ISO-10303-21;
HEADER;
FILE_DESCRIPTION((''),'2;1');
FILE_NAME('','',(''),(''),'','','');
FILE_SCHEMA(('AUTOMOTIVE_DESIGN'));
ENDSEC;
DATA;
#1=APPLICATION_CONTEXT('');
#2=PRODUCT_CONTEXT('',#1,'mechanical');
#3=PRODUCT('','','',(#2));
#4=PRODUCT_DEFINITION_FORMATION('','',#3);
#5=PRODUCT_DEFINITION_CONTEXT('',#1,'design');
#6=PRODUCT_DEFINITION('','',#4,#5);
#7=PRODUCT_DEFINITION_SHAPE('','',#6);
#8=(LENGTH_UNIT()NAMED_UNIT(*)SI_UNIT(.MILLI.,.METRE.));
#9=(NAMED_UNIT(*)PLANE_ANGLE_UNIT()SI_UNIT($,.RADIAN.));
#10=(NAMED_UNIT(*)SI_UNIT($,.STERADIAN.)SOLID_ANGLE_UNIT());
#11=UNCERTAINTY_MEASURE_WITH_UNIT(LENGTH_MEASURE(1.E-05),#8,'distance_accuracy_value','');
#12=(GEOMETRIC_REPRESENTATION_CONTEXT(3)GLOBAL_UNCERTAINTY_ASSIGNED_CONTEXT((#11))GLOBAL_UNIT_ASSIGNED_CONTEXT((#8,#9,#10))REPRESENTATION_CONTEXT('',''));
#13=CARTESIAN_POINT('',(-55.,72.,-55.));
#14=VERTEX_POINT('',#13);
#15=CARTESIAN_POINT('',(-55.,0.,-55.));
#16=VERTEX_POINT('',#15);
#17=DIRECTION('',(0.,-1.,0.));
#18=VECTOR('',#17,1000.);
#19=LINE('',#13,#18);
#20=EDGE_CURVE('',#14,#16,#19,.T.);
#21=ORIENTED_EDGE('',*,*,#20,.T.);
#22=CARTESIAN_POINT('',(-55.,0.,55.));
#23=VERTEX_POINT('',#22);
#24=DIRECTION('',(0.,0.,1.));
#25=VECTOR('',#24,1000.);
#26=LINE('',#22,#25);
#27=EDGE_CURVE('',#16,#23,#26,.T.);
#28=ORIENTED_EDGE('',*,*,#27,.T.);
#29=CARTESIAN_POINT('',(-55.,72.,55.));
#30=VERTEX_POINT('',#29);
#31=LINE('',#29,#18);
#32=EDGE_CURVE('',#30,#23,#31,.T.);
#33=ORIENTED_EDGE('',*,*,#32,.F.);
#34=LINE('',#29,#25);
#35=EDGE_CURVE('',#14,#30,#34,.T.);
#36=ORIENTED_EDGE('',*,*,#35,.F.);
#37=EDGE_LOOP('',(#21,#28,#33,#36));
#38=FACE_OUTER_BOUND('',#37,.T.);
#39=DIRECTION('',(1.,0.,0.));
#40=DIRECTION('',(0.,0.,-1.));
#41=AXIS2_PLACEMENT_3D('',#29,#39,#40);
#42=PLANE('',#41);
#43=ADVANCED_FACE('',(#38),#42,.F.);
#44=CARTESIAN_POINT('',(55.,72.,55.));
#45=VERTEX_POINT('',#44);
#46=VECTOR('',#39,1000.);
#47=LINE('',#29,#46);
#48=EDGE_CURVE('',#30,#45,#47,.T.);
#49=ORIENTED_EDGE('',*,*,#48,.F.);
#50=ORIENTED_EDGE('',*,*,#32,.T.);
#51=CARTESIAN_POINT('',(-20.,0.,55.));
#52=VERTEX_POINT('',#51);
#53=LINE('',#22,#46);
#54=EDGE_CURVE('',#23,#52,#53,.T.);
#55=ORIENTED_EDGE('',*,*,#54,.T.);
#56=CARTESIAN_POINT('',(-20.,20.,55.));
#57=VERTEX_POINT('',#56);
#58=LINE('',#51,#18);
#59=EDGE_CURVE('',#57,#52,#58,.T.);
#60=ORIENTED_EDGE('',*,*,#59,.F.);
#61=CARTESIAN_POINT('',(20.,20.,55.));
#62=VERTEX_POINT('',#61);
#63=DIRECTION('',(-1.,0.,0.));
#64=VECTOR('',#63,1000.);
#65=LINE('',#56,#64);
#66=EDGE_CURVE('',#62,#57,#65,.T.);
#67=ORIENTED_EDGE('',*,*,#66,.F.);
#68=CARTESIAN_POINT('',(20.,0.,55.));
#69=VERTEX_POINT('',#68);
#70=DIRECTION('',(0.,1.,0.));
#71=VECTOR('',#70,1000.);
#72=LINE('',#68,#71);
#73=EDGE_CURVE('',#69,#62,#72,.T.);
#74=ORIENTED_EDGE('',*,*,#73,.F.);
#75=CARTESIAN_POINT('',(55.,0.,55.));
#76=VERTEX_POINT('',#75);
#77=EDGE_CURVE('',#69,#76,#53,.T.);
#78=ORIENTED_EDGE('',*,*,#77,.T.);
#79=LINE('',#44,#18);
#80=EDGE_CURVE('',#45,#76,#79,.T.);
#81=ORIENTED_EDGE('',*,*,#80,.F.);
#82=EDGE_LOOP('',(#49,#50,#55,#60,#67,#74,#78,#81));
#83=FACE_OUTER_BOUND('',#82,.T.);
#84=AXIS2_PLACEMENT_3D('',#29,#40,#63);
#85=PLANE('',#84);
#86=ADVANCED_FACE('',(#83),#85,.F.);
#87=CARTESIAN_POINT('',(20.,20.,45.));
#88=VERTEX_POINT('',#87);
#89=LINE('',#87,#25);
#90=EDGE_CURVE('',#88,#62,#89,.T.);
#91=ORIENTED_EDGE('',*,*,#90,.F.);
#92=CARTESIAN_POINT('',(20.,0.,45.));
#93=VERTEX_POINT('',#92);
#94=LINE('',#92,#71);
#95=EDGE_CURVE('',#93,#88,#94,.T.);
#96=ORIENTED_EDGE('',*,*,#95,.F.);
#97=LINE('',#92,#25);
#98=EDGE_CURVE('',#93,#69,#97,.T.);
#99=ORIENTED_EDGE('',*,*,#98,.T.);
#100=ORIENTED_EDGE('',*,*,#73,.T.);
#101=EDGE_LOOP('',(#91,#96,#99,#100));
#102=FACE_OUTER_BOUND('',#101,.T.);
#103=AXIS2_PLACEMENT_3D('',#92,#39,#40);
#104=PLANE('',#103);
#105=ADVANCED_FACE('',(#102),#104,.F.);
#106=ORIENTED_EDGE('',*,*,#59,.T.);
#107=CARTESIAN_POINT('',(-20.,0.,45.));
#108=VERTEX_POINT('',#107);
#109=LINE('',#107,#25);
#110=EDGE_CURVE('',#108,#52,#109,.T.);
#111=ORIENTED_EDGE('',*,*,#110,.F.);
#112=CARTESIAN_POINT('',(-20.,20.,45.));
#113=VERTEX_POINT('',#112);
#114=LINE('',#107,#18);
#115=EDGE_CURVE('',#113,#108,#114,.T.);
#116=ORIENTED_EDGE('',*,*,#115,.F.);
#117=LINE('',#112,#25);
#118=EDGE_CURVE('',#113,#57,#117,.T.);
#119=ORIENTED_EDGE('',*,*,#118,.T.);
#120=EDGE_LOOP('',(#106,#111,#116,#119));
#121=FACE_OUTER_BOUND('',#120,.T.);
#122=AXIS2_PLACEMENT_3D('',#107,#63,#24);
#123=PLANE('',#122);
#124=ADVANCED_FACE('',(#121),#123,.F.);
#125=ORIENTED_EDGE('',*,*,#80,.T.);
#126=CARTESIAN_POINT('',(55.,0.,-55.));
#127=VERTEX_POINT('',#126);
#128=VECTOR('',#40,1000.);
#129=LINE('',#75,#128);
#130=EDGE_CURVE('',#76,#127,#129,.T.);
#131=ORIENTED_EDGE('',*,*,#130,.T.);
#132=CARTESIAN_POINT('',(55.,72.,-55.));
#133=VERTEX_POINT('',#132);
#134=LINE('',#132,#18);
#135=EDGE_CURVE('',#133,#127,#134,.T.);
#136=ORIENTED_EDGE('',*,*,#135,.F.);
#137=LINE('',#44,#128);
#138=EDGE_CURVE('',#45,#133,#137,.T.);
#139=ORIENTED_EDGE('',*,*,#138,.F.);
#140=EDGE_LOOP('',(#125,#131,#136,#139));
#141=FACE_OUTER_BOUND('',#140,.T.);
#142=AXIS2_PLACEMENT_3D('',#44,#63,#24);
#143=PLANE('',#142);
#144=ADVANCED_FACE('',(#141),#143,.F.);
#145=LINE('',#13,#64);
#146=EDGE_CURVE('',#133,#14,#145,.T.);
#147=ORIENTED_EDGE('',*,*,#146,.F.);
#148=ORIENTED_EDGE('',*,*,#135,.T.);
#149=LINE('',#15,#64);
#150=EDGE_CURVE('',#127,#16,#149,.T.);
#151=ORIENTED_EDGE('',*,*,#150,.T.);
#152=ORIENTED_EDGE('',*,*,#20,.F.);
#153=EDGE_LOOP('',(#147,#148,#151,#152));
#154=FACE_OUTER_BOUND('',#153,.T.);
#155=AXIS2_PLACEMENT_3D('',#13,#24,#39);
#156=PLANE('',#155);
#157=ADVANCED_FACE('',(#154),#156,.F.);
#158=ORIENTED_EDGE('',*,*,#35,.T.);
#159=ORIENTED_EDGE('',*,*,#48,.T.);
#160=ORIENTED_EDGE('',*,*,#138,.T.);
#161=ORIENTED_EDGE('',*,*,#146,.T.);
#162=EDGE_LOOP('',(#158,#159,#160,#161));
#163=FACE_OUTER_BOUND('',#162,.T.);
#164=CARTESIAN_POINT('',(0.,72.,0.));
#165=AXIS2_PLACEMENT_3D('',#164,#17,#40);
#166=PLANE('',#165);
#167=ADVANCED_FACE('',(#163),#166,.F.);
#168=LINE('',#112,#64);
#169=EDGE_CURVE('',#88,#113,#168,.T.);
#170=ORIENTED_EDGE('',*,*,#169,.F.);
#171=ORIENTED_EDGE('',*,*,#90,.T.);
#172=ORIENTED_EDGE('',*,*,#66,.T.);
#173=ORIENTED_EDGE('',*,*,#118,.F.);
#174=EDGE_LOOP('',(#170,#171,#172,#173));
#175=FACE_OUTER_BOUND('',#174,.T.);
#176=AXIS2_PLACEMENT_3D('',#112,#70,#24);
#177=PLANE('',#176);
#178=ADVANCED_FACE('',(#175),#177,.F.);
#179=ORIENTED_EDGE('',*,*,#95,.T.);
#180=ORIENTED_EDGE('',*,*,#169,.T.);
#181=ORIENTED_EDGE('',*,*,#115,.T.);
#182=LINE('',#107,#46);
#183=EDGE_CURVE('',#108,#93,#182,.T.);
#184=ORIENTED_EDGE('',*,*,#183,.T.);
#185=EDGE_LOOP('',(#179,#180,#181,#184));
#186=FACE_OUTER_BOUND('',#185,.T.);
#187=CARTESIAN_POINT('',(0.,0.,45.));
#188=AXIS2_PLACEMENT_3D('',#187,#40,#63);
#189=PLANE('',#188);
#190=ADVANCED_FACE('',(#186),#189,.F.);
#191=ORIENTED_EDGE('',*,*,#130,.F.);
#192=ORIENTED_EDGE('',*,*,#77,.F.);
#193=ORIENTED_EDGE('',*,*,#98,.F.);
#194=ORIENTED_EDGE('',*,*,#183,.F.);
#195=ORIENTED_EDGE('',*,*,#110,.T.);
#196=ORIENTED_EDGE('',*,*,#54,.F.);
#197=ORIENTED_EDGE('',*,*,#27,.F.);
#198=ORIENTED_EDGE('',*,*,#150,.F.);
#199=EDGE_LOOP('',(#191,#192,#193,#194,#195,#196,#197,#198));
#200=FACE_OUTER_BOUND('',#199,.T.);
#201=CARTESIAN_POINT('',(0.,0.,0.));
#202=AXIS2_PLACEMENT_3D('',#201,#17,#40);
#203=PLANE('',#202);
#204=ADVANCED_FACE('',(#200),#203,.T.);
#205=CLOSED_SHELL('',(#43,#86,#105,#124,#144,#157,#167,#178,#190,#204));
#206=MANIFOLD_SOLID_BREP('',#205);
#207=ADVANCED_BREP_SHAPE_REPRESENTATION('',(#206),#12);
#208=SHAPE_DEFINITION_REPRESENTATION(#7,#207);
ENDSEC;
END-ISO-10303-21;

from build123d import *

# Parameters (mm, degrees)
SKETCH1_W           = 110
SKETCH1_H           = 110
BOSS_EXTRUDE1_DEPTH = 72
SKETCH2_W           = 40
SKETCH2_H           = 20
CUT_EXTRUDE1_DEPTH  = 10


with BuildPart() as part:
    # Sketch1 → Boss-Extrude1 (new body)
    with BuildSketch(Plane(origin=(0, 0, 0), x_dir=(1, 0, 0), z_dir=(0, 1, 0))):
        Rectangle(SKETCH1_W, SKETCH1_H)
    extrude(amount=BOSS_EXTRUDE1_DEPTH)

    # Sketch2 → Cut-Extrude1 (cut)
    with BuildSketch(Plane.XY.offset(55)):
        with Locations((0, 10)):
            Rectangle(SKETCH2_W, SKETCH2_H)
    extrude(amount=-CUT_EXTRUDE1_DEPTH, mode=Mode.SUBTRACT)


solid = part.part
